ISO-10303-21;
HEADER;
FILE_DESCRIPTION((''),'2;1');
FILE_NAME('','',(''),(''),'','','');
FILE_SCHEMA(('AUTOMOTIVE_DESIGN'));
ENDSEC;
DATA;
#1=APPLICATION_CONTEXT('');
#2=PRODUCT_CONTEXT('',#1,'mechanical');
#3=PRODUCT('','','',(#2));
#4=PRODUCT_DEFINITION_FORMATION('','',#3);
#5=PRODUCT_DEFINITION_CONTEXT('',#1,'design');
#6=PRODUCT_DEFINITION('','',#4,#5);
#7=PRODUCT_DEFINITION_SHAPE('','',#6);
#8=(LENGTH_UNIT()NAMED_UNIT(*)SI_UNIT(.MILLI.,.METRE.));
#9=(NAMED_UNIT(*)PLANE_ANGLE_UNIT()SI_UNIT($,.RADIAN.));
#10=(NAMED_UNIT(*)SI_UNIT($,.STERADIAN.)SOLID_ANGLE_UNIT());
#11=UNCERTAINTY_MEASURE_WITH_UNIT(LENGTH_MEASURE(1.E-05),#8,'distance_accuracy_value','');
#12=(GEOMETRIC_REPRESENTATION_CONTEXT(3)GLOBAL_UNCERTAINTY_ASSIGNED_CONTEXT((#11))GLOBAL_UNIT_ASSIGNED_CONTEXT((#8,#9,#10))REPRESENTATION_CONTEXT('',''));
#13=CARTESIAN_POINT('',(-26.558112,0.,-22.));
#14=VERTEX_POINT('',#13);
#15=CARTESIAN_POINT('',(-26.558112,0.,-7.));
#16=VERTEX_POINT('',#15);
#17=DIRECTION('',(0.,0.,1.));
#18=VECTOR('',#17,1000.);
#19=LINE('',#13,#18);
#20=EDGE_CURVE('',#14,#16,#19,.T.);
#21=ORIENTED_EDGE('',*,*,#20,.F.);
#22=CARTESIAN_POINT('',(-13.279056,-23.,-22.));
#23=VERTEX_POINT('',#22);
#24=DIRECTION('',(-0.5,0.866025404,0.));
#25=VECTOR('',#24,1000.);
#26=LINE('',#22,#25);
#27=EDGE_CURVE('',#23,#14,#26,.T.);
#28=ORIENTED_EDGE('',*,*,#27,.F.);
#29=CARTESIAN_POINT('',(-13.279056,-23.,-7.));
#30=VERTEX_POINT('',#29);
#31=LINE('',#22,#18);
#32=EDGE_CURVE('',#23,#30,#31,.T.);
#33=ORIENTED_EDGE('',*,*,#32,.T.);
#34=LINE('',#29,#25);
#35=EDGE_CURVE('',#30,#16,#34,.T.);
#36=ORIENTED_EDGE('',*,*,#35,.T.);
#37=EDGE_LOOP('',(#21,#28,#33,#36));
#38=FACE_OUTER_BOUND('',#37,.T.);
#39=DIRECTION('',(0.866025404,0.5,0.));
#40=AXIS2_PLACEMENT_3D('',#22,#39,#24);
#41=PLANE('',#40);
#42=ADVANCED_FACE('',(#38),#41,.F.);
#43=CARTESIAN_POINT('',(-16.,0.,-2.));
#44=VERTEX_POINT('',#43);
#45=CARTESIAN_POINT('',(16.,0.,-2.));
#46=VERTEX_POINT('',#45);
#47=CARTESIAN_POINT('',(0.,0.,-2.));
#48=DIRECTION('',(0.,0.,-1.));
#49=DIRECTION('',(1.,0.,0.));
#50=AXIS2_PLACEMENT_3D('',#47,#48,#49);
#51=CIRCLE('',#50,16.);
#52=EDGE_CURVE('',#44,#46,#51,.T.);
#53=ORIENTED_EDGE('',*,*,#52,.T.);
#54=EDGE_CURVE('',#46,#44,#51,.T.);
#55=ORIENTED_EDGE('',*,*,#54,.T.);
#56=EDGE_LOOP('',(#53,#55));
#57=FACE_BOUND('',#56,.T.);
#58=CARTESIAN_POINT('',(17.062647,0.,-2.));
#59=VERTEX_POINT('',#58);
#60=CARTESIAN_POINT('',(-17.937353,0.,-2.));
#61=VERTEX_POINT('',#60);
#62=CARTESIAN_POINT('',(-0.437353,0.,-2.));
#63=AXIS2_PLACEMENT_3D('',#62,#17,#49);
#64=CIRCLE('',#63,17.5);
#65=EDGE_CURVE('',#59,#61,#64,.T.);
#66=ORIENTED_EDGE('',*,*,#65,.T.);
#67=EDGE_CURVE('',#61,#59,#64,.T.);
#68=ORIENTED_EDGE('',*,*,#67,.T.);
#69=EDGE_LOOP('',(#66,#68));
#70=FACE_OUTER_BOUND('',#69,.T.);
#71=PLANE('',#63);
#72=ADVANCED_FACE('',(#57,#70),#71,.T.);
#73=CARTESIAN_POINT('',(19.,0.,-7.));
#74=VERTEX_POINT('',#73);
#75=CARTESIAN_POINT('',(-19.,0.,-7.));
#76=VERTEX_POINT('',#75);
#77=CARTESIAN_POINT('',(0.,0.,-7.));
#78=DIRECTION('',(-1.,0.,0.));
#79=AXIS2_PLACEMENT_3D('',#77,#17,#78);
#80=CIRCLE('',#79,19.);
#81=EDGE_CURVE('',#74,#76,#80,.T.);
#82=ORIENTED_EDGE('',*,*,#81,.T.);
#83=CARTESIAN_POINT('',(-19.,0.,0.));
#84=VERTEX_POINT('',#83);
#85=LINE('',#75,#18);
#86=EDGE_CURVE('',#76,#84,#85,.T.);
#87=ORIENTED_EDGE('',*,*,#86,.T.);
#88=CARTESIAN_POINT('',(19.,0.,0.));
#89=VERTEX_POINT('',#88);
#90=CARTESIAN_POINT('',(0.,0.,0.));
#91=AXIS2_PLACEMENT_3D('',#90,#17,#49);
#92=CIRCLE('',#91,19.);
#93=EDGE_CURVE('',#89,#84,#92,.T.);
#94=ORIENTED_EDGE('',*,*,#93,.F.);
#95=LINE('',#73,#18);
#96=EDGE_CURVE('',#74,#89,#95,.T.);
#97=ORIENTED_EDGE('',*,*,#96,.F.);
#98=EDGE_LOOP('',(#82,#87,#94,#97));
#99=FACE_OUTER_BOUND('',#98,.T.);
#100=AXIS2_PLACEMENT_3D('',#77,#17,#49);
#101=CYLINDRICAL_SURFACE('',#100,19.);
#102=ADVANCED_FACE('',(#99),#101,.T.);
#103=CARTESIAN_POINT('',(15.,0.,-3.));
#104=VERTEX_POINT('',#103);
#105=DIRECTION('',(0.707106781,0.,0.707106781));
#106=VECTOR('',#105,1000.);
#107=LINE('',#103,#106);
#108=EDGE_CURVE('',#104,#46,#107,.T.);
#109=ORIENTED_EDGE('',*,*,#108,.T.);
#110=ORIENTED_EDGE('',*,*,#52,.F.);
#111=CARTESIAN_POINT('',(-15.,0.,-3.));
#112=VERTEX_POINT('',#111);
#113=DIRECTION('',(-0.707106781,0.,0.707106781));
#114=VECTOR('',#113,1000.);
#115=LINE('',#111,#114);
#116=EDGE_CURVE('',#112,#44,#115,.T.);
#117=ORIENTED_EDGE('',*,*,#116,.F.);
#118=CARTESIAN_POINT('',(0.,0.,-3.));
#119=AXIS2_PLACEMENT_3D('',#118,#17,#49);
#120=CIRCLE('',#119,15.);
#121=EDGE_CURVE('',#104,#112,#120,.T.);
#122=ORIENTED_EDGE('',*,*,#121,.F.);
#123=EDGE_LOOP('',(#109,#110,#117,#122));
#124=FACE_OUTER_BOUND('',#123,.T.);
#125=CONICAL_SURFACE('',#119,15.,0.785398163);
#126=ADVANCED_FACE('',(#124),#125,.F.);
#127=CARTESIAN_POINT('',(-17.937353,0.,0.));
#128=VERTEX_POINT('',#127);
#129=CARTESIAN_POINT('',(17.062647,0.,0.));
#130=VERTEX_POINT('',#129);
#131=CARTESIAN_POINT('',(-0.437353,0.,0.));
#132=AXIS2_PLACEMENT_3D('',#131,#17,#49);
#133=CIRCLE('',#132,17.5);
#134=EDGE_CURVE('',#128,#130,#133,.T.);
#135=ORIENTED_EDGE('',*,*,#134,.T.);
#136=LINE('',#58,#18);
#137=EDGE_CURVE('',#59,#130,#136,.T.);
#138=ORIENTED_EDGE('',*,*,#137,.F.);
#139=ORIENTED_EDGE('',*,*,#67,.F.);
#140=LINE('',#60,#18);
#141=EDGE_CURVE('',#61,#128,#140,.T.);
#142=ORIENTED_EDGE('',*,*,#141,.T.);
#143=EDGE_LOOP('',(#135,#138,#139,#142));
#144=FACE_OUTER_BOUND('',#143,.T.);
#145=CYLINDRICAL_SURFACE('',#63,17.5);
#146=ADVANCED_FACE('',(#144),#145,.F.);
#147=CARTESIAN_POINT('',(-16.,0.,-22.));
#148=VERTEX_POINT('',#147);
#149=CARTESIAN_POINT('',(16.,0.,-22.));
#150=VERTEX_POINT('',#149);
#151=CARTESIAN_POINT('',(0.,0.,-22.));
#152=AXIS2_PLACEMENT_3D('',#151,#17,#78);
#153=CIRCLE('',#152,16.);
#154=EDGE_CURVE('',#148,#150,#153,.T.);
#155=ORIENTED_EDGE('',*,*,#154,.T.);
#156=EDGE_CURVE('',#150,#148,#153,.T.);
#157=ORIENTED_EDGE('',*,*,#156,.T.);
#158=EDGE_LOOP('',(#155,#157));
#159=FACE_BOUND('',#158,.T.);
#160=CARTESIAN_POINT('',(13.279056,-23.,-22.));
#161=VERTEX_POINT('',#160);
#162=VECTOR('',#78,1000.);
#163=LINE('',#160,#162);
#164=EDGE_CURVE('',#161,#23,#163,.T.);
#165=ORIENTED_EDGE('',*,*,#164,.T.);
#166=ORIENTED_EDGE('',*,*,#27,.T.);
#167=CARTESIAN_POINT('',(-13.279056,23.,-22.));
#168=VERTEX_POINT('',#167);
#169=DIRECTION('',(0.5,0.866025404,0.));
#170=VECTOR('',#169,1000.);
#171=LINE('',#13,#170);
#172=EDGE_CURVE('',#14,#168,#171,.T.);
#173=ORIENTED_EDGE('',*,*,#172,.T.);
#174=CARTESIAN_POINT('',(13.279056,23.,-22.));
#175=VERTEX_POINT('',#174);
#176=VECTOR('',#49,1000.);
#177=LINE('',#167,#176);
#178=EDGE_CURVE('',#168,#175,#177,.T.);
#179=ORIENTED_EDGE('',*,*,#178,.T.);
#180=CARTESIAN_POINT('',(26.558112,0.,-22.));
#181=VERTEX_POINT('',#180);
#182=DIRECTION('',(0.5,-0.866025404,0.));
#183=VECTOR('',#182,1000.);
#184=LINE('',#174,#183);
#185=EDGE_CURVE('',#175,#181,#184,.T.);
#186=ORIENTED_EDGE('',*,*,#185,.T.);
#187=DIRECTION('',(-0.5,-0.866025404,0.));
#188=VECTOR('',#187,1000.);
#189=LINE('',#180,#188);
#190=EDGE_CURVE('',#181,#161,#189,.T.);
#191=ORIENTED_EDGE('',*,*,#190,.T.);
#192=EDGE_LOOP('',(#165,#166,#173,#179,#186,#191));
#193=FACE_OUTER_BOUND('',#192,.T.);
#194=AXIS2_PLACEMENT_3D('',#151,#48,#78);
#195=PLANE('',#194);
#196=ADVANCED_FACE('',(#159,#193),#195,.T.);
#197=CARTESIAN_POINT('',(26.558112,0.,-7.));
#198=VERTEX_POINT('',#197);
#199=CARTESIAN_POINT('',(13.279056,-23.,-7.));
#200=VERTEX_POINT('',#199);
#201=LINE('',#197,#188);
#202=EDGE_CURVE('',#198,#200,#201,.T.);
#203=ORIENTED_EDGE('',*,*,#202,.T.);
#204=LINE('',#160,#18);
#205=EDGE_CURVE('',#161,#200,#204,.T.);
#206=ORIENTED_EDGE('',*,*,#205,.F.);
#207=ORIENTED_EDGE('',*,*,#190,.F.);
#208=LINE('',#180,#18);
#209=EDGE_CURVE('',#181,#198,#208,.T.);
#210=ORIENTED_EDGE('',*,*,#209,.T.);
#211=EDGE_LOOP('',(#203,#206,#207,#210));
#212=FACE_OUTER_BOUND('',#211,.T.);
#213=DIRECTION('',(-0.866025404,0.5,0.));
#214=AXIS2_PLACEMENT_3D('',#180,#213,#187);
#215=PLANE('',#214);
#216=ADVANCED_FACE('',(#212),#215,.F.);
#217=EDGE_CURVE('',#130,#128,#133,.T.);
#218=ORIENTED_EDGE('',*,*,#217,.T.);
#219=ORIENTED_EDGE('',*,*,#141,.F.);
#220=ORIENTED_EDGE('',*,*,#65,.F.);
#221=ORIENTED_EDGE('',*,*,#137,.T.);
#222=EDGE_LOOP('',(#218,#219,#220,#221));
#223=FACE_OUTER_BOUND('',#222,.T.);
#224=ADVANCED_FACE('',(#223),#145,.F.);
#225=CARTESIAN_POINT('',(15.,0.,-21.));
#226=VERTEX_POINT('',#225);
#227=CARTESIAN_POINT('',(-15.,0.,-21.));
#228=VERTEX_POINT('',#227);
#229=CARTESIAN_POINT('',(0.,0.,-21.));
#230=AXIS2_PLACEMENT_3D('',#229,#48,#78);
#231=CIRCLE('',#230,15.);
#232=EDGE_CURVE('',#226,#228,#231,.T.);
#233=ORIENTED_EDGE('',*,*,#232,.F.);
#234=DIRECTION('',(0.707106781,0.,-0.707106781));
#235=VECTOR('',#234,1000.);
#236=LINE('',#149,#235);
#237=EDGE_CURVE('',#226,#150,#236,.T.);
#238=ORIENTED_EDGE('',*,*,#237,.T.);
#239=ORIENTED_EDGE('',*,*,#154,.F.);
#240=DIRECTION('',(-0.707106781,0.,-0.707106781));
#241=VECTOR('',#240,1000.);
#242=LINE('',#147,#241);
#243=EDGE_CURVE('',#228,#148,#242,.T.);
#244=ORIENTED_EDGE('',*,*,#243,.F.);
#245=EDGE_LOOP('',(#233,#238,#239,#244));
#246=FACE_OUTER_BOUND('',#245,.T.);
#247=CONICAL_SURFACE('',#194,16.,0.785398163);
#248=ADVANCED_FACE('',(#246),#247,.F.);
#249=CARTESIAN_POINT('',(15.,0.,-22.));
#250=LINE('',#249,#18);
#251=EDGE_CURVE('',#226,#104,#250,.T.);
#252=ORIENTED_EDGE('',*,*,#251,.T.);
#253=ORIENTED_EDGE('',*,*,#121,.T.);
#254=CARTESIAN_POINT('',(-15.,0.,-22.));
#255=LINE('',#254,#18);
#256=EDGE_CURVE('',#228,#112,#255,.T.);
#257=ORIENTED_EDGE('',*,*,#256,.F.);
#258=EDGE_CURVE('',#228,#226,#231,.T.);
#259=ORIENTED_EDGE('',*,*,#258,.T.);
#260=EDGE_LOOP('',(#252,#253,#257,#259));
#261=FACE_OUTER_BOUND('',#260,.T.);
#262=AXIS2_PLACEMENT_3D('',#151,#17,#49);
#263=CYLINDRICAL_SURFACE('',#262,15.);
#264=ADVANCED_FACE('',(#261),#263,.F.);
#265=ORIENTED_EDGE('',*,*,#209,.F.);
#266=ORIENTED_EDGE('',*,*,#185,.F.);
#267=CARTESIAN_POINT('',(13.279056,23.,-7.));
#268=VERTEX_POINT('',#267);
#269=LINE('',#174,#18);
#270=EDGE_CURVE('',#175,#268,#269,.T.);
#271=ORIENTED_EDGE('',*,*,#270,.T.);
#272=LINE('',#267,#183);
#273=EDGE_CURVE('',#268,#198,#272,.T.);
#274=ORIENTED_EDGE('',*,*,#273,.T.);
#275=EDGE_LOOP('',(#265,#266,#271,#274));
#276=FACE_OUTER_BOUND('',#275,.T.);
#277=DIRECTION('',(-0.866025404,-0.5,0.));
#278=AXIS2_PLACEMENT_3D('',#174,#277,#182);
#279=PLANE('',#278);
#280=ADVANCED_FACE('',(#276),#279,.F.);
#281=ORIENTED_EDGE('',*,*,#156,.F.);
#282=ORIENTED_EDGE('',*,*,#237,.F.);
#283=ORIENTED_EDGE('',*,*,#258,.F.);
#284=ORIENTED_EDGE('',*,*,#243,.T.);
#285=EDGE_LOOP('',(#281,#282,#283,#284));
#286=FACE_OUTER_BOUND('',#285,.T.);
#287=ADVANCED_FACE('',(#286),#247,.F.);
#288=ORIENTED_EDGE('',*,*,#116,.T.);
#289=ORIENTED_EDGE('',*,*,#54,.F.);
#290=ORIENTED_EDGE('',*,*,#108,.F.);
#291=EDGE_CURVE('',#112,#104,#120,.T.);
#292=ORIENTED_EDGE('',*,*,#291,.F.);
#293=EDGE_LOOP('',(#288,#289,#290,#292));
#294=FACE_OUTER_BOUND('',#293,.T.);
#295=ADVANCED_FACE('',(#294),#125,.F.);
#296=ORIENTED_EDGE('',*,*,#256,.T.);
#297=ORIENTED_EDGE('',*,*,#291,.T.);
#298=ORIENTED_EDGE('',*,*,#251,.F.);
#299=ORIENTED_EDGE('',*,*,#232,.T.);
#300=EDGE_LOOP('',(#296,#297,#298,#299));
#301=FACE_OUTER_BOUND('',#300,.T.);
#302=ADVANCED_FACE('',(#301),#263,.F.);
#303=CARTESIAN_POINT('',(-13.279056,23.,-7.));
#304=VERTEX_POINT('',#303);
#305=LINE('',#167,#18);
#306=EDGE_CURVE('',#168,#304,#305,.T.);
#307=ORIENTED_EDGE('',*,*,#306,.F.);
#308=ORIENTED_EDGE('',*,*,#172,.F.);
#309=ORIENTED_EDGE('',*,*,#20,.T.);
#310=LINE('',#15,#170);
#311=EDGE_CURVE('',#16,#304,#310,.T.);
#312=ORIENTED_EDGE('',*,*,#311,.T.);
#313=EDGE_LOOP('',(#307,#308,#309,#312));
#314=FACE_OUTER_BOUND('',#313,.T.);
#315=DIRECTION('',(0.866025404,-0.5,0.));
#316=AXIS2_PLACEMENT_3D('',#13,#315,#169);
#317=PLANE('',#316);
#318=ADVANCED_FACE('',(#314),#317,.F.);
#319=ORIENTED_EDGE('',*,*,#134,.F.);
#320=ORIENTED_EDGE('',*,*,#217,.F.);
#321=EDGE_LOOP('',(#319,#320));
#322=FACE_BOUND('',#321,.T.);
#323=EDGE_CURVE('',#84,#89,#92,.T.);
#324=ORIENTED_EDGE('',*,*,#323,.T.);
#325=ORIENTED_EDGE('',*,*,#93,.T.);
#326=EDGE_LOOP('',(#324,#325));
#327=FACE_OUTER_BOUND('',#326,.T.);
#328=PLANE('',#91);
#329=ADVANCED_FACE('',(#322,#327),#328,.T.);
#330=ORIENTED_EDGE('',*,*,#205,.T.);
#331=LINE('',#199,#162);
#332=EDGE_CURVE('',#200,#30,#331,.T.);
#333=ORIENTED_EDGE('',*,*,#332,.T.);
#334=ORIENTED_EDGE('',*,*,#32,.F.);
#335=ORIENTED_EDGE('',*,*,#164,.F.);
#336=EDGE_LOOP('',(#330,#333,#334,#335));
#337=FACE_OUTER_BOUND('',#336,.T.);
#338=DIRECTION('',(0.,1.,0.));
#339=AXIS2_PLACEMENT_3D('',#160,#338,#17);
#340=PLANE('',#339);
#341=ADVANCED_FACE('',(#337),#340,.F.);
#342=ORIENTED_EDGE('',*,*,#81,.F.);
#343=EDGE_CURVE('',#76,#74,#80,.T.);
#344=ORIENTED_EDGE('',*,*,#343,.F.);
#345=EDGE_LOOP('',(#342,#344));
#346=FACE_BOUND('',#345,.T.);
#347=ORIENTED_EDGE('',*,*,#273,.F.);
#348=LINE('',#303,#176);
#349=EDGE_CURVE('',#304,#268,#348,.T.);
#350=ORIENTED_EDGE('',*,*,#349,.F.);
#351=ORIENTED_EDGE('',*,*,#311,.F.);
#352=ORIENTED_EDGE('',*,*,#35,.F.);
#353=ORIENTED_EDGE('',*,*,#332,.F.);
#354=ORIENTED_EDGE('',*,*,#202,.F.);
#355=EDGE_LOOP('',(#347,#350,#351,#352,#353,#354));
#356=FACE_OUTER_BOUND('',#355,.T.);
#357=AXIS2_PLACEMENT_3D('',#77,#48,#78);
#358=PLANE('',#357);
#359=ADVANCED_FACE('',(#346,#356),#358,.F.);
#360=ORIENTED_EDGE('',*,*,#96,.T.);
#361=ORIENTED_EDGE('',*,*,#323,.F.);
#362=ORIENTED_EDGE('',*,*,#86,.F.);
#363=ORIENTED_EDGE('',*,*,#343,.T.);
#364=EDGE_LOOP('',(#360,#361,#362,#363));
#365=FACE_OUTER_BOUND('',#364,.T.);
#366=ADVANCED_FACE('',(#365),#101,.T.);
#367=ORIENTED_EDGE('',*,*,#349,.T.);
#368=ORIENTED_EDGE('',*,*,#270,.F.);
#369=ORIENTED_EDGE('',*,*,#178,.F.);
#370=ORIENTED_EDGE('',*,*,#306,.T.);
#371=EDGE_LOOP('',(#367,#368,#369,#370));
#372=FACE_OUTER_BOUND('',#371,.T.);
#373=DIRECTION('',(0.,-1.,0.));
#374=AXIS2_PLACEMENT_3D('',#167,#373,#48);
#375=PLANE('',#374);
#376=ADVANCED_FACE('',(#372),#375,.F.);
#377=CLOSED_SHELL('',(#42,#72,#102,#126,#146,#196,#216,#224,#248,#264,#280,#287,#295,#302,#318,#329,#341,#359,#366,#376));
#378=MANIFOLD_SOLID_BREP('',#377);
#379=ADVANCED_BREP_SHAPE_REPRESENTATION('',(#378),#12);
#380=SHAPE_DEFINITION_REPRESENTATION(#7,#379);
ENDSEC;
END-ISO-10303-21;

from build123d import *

# Parameters (mm, degrees)
SKETCH_1_R          = 19
EXTRUDE_1_DEPTH     = 7
EXTRUDE_2_DEPTH     = 15
SKETCH_3_R          = 17.5
CUT_EXTRUDE_1_DEPTH = 2
SKETCH_4_R          = 15
CUT_EXTRUDE_2_DEPTH = 41.426888742
CHAMFER_1_SIZE      = 1


with BuildPart() as part:
    # 草图1 → 凸台-拉伸1 (new body)
    with BuildSketch(Plane.XY):
        Circle(SKETCH_1_R)
    extrude(amount=-EXTRUDE_1_DEPTH)

    # 草图2 → 凸台-拉伸2 (add)
    with BuildSketch(Plane(origin=(0, 0, -7), x_dir=(-1, 0, 0), z_dir=(0, 0, -1))):
        Polygon((13.279056191, -23), (26.558112383, 0), (13.279056191, 23), (-13.279056191, 23), (-26.558112383, 0), (-13.279056191, -23), align=None)
    extrude(amount=EXTRUDE_2_DEPTH)

    # 草图3 → 切除-拉伸1 (cut)
    with BuildSketch(Plane.XY):
        with Locations((-0.437352874, 0)):
            Circle(SKETCH_3_R)
    extrude(amount=-CUT_EXTRUDE_1_DEPTH, mode=Mode.SUBTRACT)

    # 草图4 → 切除-拉伸2 (cut, through all)
    with BuildSketch(Plane.XY.offset(-2)):
        Circle(SKETCH_4_R)
    extrude(amount=-CUT_EXTRUDE_2_DEPTH, mode=Mode.SUBTRACT)

    # 倒角1
    chamfer_1_edges = [part.edges().sort_by_distance(p)[0] for p in [
        (-15, 0, -22),
        (-15, 0, -2),
    ]]
    chamfer(chamfer_1_edges, length=CHAMFER_1_SIZE)


solid = part.part
